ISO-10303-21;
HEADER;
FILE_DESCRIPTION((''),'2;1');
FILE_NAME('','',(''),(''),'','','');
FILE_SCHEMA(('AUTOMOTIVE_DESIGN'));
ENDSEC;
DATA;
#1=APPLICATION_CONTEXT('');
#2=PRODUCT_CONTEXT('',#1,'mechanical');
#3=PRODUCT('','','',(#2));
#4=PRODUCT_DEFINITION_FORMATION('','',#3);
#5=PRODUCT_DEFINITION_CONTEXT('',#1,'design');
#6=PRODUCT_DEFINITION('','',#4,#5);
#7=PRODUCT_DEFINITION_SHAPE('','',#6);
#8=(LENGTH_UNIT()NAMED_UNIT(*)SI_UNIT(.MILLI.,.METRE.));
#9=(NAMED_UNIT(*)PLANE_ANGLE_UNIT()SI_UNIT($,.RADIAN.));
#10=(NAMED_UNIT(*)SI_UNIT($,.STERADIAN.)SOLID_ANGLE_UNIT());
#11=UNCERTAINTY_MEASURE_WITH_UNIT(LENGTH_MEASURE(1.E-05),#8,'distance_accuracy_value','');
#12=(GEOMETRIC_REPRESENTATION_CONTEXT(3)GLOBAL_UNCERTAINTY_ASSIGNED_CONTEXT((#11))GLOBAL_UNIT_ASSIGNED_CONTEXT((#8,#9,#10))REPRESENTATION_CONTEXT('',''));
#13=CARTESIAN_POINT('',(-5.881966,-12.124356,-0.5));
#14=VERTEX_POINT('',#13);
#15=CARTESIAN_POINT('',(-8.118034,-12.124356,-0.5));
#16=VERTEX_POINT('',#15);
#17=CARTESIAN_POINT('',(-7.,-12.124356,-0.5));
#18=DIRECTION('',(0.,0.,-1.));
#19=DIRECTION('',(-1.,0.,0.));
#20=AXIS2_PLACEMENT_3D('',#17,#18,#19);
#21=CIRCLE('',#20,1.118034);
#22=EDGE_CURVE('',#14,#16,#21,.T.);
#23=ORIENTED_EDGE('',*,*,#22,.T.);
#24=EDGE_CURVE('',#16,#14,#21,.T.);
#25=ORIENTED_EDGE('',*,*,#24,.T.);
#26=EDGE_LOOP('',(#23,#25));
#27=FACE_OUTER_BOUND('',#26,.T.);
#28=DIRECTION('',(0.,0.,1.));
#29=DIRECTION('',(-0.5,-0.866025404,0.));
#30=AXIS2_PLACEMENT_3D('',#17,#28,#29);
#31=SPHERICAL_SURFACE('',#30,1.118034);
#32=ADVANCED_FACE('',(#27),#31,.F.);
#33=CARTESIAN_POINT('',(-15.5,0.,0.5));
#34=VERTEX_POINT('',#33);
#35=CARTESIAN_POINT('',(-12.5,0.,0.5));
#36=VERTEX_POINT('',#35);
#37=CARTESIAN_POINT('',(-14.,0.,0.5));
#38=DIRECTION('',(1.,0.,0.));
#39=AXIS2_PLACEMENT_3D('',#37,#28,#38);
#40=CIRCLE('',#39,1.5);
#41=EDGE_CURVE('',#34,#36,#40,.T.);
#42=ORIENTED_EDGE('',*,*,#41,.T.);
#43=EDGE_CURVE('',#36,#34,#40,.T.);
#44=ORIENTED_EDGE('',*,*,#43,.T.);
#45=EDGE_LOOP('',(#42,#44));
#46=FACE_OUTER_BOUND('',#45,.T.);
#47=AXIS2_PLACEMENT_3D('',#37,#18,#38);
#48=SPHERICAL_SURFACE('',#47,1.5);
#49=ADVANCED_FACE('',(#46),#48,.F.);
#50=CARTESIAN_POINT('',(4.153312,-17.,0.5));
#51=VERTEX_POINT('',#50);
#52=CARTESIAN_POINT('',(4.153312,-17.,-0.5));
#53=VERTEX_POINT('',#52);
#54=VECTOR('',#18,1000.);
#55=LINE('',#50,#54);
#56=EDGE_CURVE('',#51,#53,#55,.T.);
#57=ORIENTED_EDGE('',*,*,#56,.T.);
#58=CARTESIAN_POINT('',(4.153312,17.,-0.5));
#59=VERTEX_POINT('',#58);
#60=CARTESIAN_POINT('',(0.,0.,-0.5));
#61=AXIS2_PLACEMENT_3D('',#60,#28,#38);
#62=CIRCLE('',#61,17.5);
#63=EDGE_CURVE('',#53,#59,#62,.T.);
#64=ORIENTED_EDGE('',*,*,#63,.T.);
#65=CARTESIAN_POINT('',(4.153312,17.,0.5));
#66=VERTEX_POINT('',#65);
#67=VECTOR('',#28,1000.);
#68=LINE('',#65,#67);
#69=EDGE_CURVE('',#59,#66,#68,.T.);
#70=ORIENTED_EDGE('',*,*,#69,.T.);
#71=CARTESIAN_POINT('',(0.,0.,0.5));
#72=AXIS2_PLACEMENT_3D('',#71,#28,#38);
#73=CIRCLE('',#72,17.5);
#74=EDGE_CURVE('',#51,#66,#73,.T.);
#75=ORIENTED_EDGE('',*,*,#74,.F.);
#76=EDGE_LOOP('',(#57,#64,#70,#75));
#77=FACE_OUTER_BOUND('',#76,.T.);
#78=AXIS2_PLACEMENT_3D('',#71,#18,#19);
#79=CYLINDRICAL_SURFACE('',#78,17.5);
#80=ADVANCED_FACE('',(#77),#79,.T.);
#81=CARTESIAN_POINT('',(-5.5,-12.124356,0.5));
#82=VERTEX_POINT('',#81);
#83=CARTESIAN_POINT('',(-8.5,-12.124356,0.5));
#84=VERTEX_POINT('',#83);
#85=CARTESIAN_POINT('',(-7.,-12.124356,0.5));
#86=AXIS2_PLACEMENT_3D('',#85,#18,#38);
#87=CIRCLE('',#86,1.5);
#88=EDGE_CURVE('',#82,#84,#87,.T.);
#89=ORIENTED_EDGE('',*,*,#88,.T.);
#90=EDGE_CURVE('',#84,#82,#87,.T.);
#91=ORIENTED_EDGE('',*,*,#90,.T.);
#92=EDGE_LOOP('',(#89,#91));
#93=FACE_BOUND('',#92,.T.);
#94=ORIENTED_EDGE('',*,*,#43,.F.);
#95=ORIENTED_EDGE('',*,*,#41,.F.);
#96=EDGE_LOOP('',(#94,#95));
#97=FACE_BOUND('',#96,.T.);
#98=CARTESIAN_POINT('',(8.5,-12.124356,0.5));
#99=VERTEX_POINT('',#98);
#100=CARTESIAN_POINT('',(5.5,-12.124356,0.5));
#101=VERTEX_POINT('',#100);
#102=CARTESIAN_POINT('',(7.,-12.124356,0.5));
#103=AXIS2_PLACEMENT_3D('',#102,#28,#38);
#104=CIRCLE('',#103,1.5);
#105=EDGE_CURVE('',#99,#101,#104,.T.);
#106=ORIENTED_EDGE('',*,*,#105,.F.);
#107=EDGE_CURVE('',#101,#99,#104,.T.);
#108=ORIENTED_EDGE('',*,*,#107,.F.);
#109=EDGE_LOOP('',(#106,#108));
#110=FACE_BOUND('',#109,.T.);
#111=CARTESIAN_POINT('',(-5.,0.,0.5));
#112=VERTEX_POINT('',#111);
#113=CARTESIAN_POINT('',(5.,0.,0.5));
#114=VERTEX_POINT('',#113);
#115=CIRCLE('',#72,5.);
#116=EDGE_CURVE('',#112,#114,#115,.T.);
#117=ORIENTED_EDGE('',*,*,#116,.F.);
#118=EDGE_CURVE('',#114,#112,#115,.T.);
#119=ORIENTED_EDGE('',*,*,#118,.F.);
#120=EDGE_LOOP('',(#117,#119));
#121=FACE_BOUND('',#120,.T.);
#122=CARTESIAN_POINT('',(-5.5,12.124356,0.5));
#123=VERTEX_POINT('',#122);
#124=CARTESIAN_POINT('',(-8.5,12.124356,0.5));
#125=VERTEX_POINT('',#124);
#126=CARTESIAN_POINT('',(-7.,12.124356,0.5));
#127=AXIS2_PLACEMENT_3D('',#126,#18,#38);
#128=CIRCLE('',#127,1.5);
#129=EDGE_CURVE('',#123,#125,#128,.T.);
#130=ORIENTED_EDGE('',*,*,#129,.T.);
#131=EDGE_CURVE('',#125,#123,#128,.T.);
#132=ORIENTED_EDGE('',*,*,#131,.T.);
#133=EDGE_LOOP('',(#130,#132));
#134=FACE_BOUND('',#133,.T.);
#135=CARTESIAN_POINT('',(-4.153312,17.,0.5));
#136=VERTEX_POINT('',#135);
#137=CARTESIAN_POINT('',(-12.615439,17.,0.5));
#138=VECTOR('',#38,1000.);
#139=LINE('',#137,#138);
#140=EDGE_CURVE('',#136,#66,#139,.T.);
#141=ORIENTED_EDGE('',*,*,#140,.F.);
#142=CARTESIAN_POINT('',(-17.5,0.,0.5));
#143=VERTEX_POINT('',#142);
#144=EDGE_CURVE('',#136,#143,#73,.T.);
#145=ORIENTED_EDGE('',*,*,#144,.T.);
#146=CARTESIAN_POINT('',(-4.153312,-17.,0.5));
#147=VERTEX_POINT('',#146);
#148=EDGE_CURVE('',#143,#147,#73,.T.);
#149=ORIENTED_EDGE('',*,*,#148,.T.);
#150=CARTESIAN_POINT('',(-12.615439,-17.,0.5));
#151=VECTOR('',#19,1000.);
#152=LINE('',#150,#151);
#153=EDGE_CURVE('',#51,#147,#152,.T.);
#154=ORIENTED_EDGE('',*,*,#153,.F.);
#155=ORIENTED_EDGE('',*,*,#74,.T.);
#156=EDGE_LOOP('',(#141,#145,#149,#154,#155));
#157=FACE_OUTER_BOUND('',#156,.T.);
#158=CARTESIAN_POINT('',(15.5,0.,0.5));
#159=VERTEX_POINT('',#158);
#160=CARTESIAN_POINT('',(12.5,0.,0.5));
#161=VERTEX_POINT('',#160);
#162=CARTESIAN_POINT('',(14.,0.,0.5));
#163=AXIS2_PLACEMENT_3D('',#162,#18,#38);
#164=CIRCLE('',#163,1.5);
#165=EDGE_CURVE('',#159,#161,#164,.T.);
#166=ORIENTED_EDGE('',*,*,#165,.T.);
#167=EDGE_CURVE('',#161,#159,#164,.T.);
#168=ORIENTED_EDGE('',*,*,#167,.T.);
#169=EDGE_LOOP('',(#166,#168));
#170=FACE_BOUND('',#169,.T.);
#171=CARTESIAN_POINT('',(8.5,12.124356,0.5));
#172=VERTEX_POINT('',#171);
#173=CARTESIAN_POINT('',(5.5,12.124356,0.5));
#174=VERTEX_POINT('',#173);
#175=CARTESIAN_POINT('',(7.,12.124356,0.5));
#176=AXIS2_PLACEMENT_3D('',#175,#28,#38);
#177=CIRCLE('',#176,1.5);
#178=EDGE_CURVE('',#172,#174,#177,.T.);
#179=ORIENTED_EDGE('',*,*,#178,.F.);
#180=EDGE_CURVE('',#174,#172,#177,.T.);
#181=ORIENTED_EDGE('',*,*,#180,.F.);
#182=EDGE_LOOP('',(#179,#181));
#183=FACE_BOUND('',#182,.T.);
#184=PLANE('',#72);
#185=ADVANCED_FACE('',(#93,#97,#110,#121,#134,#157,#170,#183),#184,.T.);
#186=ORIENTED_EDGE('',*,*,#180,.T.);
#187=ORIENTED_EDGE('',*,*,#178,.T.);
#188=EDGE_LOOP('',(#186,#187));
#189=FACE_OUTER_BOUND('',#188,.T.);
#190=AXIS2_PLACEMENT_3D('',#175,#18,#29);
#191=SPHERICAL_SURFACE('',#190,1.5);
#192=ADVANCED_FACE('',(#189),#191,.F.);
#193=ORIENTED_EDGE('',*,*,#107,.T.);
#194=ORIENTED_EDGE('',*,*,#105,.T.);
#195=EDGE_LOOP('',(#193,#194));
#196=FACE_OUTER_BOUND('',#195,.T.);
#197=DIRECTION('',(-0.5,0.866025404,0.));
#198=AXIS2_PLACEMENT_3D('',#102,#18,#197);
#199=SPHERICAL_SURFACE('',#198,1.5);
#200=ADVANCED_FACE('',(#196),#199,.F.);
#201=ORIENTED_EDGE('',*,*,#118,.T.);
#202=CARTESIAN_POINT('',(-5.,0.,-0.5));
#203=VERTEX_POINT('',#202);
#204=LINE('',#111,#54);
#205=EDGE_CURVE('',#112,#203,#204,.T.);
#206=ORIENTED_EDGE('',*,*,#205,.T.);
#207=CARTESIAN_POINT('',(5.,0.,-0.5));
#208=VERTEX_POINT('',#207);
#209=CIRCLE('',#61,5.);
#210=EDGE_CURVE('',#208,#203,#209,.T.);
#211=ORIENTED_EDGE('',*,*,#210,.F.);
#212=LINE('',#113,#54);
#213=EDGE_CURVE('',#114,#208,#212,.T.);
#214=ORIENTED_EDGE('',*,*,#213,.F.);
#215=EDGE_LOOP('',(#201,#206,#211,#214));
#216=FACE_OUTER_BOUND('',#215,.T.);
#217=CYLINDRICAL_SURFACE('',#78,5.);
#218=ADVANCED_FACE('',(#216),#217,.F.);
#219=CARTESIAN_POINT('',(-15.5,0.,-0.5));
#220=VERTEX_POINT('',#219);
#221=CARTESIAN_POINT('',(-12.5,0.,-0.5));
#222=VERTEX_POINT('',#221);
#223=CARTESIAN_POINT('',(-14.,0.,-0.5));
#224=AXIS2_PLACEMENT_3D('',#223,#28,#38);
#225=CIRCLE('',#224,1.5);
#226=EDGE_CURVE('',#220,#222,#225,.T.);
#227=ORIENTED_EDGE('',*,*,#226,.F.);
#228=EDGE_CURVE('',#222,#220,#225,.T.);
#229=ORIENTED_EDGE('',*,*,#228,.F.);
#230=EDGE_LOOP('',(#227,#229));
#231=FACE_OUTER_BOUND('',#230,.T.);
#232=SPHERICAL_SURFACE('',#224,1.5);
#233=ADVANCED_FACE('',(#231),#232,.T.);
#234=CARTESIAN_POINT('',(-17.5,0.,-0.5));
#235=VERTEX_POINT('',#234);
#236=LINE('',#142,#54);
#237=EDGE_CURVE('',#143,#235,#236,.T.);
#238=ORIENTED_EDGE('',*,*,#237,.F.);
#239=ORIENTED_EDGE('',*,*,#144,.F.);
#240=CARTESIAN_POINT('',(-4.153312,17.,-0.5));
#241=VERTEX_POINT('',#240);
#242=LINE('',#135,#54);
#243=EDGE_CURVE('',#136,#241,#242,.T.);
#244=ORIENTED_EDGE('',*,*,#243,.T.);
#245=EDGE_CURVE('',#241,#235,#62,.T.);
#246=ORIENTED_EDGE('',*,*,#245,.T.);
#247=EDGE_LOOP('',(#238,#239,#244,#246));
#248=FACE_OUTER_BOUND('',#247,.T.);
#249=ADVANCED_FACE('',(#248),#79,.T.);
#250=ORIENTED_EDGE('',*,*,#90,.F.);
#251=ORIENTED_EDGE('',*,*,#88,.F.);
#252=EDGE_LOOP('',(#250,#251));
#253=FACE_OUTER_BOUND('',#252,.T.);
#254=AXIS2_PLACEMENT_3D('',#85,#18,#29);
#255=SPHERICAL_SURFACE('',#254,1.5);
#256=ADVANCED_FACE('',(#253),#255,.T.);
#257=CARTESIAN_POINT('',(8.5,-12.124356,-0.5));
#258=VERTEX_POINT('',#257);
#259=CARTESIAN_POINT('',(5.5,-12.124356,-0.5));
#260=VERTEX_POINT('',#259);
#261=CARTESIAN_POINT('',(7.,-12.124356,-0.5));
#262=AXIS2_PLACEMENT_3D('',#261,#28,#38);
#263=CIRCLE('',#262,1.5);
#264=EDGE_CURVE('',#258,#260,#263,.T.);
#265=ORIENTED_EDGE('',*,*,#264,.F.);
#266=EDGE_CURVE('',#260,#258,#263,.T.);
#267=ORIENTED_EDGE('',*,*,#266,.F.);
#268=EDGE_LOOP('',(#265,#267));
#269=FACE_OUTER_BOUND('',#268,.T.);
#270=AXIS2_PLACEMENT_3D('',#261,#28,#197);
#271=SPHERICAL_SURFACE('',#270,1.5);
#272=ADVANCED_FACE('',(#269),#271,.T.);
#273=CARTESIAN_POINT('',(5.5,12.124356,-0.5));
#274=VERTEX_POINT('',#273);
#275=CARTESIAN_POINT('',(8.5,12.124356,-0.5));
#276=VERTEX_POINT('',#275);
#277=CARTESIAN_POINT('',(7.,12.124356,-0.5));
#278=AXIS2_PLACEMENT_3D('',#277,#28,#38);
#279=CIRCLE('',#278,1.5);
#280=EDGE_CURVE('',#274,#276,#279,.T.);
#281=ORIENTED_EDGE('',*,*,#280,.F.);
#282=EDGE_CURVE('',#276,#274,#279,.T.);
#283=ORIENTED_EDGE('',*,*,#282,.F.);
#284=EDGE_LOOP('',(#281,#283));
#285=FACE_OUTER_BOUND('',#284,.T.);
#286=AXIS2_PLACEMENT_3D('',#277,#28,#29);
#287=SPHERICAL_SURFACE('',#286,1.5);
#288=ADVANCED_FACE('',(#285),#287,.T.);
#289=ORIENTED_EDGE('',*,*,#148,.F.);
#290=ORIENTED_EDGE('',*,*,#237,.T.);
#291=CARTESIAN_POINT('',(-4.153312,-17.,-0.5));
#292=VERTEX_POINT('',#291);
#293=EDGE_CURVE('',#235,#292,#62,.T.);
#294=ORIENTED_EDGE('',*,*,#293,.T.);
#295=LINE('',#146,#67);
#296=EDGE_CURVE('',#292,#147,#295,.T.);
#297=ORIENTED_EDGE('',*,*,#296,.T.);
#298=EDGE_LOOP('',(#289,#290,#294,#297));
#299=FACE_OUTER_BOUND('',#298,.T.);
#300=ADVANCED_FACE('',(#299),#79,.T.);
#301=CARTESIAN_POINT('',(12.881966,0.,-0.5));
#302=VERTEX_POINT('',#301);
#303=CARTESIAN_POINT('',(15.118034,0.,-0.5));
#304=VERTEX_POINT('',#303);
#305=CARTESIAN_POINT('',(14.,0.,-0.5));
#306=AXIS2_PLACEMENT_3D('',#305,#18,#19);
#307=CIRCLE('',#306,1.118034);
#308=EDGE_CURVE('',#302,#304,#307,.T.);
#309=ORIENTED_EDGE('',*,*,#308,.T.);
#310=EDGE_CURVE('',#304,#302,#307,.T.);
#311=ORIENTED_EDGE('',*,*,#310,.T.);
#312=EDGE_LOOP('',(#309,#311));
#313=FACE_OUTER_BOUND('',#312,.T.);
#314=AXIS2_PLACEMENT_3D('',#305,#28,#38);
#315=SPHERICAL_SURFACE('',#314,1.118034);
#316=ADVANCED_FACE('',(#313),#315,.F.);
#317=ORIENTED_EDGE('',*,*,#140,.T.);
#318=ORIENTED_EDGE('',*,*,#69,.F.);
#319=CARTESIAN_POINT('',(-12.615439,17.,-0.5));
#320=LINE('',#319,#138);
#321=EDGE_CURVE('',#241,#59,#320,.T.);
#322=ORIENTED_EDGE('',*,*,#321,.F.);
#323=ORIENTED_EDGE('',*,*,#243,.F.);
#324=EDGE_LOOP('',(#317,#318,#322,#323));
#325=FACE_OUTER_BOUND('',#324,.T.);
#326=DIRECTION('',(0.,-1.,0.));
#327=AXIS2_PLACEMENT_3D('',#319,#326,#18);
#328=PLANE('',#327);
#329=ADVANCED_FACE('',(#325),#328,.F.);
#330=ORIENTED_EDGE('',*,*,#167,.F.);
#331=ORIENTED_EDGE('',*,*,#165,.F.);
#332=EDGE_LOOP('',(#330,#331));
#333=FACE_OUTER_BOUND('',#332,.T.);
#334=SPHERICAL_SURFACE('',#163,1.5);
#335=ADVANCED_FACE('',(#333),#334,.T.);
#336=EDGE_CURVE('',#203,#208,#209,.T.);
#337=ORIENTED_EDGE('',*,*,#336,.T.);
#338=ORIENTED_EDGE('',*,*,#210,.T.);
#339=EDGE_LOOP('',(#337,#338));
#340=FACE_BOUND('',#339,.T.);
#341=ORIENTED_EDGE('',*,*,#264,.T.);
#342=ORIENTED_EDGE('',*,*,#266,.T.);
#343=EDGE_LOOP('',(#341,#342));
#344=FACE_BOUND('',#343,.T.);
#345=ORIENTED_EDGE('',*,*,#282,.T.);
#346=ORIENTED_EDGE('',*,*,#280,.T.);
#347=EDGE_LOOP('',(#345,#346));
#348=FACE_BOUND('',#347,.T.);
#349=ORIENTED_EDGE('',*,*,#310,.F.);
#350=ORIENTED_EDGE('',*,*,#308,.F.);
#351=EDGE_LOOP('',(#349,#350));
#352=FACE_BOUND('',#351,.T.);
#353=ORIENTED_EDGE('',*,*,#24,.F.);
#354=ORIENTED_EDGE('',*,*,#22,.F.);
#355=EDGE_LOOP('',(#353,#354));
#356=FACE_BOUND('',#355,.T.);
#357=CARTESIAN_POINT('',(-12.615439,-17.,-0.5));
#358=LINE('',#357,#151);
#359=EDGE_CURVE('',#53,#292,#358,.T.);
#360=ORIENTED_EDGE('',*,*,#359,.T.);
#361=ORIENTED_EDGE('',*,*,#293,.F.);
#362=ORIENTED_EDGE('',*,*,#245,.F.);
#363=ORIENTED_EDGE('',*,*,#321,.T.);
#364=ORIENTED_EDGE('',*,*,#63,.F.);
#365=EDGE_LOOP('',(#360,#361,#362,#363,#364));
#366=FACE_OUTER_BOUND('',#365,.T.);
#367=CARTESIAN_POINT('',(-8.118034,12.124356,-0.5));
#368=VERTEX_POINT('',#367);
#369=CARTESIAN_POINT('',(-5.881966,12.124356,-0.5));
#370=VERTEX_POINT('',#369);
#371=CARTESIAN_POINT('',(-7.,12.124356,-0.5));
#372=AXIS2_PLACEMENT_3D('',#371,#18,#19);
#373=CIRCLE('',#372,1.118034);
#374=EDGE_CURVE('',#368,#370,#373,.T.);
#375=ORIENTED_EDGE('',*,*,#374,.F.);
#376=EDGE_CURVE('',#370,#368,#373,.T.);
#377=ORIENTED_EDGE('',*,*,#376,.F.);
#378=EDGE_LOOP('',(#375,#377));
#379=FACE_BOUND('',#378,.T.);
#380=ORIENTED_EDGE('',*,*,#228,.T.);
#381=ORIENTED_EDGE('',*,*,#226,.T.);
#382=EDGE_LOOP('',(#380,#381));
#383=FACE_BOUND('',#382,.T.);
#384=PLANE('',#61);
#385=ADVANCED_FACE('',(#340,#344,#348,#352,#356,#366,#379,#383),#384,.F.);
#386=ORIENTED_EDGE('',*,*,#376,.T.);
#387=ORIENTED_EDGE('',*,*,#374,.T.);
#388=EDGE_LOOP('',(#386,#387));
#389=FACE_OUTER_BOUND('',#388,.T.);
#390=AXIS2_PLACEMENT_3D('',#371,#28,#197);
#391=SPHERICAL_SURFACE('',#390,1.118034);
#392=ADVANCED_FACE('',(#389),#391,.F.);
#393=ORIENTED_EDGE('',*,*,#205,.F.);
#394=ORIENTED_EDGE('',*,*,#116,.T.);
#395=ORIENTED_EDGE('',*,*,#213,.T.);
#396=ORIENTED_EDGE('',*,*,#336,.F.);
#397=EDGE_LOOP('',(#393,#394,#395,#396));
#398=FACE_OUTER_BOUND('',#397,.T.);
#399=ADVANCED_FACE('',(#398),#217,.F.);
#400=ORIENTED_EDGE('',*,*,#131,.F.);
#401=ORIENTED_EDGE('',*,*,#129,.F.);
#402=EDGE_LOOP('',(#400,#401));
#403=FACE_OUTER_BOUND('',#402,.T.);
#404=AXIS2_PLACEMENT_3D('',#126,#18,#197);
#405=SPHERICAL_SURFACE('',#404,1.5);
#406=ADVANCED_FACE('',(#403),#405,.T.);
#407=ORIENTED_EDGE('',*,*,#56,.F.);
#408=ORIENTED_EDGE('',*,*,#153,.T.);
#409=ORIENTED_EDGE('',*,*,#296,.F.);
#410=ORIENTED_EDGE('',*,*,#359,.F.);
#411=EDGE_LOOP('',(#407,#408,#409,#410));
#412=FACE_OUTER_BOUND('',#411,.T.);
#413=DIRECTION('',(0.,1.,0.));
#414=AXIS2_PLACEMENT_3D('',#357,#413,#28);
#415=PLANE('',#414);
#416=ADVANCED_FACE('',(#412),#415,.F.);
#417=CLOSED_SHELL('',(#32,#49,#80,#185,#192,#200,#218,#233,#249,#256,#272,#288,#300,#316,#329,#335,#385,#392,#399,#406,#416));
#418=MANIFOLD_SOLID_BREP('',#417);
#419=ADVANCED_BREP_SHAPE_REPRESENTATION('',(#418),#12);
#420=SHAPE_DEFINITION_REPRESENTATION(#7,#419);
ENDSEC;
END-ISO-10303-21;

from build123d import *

# Parameters (mm, degrees)
SKETCH1_R           = 17.5
SKETCH1_R_2         = 5
BOSS_EXTRUDE1_DEPTH = 0.5
SKETCH2_W           = 25.230878588
SKETCH2_H           = 11.302160125
SKETCH2_H_2         = 10.824604063
CUT_EXTRUDE1_DEPTH  = 1
CIRPATTERN1_COUNT   = 3
CIRPATTERN2_COUNT   = 3
CIRPATTERN3_COUNT   = 3
CIRPATTERN4_COUNT   = 3


with BuildPart() as part:
    # Sketch1 → Boss-Extrude1 (new, symmetric)
    with BuildSketch(Plane.XY):
        Circle(SKETCH1_R)
        Circle(SKETCH1_R_2, mode=Mode.SUBTRACT)
    extrude(amount=BOSS_EXTRUDE1_DEPTH, both=True)

    # Sketch2 → Cut-Extrude1 (cut)
    with BuildSketch(Plane.XY.offset(0.5)):
        with Locations((0, 22.651080063)):
            Rectangle(SKETCH2_W, SKETCH2_H)
        with Locations((0, -22.412302032)):
            Rectangle(SKETCH2_W, SKETCH2_H_2)
    extrude(amount=-CUT_EXTRUDE1_DEPTH, mode=Mode.SUBTRACT)

    # Sketch3 → Revolve1 (revolve)
    with BuildSketch(Plane.XY.offset(0.5)):
        with BuildLine():
            Line((14, 1.5), (14, -1.5))
            ThreePointArc((14, -1.5), (15.5, 0), (14, 1.5))
        make_face()
    revolve1 = revolve(axis=Axis((14, 1.5, 0.5), (0, -1, 0)))

    # CirPattern1: Revolve1 ×3 about axis
    cirpattern1_axis = Axis((0, 0, 0), (0, 0, 1))
    for i in range(1, CIRPATTERN1_COUNT):
        add(revolve1.rotate(cirpattern1_axis, i * 360 / CIRPATTERN1_COUNT))

    # Sketch5 → Revolve2 (revolve)
    with BuildSketch(Plane(origin=(0, 0, -0.5), x_dir=(-1, 0, 0), z_dir=(0, 0, -1))):
        with BuildLine():
            Line((14, -1.5), (14, 1.5))
            ThreePointArc((14, 1.5), (15.5, 0), (14, -1.5))
        make_face()
    revolve2 = revolve(axis=Axis((-14, -1.5, -0.5), (0, 1, 0)))

    # CirPattern2: Revolve2 ×3 about axis
    cirpattern2_axis = Axis((0, 0, 0), (0, 0, 1))
    for i in range(1, CIRPATTERN2_COUNT):
        add(revolve2.rotate(cirpattern2_axis, i * 360 / CIRPATTERN2_COUNT))

    # Sketch6 → Cut-Revolve2 (revolve, cut)
    with BuildSketch(Plane.XY.offset(0.5)):
        with BuildLine():
            Line((-14, 1.5), (-14, -1.5))
            ThreePointArc((-14, -1.5), (-15.5, 0), (-14, 1.5))
        make_face()
    cut_revolve2 = revolve(axis=Axis((-14, 1.5, 0.5), (0, -1, 0)), mode=Mode.SUBTRACT)

    # CirPattern3: Cut-Revolve2 ×3 about axis
    cirpattern3_axis = Axis((0, 0, 0), (0, 0, 1))
    for i in range(1, CIRPATTERN3_COUNT):
        add(cut_revolve2.rotate(cirpattern3_axis, i * 360 / CIRPATTERN3_COUNT), mode=Mode.SUBTRACT)

    # Sketch7 → Cut-Revolve3 (revolve, cut)
    with BuildSketch(Plane(origin=(0, 0, -0.5), x_dir=(-1, 0, 0), z_dir=(0, 0, -1))):
        with BuildLine():
            Line((-14, -1.118033989), (-14, 1.118033989))
            ThreePointArc((-14, 1.118033989), (-15.118033989, 0), (-14, -1.118033989))
        make_face()
    cut_revolve3 = revolve(axis=Axis((14, -1.118033989, -0.5), (0, 1, 0)), mode=Mode.SUBTRACT)

    # CirPattern4: Cut-Revolve3 ×3 about axis
    cirpattern4_axis = Axis((0, 0, 0), (0, 0, 1))
    for i in range(1, CIRPATTERN4_COUNT):
        add(cut_revolve3.rotate(cirpattern4_axis, i * 360 / CIRPATTERN4_COUNT), mode=Mode.SUBTRACT)


solid = part.part
